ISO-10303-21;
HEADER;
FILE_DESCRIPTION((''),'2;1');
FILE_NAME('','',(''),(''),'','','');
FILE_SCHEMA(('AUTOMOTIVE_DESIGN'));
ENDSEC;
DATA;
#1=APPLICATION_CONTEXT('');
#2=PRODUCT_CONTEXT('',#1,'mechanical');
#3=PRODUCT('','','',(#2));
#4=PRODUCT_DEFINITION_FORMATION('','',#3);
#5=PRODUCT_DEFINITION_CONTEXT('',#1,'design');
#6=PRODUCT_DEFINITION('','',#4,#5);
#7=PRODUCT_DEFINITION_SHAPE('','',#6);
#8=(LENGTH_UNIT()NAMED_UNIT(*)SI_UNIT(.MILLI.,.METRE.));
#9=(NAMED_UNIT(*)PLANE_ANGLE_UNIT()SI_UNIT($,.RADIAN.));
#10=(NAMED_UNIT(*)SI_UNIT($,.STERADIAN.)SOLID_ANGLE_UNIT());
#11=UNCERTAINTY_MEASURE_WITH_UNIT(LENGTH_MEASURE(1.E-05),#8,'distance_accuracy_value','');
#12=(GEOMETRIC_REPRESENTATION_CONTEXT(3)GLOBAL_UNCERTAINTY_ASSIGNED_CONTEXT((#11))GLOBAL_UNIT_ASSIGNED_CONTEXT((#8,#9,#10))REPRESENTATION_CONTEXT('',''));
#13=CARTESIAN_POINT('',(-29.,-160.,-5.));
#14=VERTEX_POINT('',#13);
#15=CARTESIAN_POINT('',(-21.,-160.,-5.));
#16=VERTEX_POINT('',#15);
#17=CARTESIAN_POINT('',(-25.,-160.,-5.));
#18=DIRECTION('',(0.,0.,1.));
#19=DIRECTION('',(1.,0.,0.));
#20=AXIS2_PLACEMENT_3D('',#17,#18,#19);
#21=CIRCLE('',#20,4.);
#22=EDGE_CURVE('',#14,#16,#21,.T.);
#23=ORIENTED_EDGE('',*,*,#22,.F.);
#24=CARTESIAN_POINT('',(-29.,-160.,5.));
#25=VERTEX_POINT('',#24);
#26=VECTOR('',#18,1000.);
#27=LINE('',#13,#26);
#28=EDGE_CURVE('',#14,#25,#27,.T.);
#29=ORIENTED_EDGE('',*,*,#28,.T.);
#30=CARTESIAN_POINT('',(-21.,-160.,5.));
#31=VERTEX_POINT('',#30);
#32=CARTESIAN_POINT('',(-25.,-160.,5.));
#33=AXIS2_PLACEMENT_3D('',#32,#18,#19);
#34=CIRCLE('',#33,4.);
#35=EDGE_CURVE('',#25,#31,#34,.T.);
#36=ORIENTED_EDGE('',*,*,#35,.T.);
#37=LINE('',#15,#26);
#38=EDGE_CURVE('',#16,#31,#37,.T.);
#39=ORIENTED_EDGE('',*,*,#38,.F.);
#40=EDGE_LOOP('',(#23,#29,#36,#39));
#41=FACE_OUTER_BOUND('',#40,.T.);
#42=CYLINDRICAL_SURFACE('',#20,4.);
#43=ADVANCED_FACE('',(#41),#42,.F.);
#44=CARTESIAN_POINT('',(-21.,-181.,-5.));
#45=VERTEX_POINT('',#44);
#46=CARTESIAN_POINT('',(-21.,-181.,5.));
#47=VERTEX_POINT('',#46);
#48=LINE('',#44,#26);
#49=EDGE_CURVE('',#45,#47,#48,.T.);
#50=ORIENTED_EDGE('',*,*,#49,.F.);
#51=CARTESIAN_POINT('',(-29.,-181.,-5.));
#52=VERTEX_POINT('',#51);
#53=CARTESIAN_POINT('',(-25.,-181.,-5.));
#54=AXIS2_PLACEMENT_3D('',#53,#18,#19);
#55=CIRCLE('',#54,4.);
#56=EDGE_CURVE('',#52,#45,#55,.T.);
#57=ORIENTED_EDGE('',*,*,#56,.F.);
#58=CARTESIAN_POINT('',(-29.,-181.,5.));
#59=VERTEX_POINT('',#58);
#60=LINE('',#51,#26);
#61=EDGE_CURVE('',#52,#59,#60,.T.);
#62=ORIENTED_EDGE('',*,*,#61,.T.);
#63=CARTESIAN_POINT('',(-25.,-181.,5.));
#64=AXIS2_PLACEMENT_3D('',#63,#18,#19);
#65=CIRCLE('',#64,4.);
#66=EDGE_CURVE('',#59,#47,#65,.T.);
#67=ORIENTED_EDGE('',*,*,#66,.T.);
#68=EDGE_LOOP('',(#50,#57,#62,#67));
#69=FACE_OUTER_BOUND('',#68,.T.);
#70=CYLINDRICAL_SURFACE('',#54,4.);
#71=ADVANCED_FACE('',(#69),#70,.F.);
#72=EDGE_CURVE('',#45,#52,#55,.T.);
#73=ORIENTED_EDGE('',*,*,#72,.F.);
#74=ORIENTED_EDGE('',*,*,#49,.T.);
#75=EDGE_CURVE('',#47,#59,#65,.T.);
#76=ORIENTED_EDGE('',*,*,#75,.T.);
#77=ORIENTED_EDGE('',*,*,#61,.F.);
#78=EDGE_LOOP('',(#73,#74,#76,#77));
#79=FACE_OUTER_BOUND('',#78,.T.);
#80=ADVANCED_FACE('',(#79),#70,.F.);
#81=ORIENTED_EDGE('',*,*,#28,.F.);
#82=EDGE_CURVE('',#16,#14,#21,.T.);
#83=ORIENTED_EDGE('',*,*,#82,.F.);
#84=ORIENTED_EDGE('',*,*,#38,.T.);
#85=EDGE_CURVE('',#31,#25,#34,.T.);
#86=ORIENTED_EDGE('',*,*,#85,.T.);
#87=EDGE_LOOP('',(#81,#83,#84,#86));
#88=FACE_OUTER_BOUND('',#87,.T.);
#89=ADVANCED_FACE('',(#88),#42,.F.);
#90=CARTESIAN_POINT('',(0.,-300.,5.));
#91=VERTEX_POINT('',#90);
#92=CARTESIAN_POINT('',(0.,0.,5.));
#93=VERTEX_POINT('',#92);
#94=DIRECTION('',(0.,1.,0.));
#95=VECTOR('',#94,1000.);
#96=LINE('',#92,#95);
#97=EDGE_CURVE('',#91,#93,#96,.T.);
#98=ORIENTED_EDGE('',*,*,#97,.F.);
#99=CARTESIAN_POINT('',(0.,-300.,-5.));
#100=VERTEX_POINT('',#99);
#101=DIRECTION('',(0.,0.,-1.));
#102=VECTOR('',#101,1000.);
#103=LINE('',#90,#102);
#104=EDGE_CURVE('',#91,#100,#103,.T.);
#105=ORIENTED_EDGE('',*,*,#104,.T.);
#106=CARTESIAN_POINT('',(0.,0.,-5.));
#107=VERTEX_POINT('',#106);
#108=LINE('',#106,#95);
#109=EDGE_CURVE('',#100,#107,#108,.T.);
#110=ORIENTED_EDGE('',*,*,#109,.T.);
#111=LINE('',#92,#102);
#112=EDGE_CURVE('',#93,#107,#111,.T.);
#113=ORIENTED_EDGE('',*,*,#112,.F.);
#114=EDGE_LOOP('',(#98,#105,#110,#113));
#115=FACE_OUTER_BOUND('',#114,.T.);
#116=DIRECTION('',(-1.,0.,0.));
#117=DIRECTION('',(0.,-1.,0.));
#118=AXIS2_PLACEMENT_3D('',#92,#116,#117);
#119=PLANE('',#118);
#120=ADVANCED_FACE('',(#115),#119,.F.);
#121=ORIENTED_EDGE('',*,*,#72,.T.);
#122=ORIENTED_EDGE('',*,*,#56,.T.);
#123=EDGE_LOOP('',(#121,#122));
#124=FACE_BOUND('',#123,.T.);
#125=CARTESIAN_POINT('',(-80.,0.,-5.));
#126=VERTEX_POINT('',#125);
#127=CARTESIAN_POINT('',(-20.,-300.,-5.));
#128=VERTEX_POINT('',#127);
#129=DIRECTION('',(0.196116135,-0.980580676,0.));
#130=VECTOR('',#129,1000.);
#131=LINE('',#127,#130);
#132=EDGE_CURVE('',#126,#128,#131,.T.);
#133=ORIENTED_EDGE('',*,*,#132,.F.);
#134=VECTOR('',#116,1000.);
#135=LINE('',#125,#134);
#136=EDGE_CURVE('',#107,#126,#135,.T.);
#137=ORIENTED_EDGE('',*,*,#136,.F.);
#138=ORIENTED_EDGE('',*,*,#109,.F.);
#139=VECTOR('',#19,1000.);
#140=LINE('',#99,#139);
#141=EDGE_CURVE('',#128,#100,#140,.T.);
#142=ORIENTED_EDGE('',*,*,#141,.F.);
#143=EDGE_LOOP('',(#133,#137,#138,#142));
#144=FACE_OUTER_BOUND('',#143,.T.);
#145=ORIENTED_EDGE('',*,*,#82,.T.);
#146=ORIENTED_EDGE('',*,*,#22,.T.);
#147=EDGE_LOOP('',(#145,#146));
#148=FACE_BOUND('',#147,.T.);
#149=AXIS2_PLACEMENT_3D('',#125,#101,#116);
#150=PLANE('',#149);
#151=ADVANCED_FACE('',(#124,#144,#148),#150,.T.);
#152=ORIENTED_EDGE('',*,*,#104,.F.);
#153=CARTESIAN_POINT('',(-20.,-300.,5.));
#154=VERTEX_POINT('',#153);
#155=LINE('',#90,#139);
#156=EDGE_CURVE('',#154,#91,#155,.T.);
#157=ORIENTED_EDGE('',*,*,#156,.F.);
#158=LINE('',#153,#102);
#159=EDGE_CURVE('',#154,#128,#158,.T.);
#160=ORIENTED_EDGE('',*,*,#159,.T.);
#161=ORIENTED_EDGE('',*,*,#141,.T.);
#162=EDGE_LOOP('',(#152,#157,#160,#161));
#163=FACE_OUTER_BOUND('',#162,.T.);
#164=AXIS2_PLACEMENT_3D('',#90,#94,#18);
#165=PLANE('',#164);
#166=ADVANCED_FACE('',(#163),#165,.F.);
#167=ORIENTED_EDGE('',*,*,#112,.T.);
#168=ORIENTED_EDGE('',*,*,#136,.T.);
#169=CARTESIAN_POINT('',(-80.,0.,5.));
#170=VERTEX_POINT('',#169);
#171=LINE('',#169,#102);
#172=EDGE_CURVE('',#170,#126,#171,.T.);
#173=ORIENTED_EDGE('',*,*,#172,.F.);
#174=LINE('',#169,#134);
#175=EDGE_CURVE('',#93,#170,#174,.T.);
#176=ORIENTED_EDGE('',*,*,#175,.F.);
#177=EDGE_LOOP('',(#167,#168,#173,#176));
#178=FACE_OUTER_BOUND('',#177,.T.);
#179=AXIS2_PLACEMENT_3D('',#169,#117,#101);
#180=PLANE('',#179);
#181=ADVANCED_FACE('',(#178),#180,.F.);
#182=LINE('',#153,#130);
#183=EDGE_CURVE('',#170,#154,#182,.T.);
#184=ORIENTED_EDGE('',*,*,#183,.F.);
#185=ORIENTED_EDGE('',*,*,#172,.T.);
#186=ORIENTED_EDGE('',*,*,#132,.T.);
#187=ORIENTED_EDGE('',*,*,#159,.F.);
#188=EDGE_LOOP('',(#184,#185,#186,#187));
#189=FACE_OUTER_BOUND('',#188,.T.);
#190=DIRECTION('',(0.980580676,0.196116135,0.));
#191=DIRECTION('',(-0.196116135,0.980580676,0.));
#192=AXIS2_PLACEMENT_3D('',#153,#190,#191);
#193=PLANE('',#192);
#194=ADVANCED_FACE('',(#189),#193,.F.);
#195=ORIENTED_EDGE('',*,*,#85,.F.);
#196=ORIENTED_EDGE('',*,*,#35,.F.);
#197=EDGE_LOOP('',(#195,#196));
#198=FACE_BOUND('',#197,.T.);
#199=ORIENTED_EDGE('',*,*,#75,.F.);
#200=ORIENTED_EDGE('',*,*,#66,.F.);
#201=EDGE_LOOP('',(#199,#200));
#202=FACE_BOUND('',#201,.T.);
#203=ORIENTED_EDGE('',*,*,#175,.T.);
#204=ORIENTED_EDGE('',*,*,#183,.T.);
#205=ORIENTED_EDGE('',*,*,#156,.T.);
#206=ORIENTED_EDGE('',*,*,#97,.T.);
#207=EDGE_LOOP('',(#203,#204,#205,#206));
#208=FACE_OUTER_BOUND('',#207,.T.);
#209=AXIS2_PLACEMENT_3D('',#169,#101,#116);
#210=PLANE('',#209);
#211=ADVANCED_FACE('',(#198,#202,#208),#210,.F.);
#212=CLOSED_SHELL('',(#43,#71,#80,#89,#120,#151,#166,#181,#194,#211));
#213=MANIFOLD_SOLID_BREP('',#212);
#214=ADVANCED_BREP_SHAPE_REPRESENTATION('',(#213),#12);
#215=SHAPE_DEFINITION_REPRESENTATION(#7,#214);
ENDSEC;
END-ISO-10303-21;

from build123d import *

# Parameters (mm, degrees)
EXTRUDE1_DEPTH = 5
SKETCH2_R      = 4
EXTRUDE2_DEPTH = 10


with BuildPart() as part:
    # Sketch1 → Extrude1 (new, symmetric)
    with BuildSketch(Plane.XY):
        Polygon((-80, 0), (0, 0), (0, -300), (-20, -300), align=None)
    extrude(amount=EXTRUDE1_DEPTH, both=True)

    # Sketch2 → Extrude2 (cut)
    with BuildSketch(Plane.XY.offset(5)):
        with Locations((-25, -160)):
            Circle(SKETCH2_R)
        with Locations((-25, -181)):
            Circle(SKETCH2_R)
    extrude(amount=-EXTRUDE2_DEPTH, mode=Mode.SUBTRACT)


solid = part.part
